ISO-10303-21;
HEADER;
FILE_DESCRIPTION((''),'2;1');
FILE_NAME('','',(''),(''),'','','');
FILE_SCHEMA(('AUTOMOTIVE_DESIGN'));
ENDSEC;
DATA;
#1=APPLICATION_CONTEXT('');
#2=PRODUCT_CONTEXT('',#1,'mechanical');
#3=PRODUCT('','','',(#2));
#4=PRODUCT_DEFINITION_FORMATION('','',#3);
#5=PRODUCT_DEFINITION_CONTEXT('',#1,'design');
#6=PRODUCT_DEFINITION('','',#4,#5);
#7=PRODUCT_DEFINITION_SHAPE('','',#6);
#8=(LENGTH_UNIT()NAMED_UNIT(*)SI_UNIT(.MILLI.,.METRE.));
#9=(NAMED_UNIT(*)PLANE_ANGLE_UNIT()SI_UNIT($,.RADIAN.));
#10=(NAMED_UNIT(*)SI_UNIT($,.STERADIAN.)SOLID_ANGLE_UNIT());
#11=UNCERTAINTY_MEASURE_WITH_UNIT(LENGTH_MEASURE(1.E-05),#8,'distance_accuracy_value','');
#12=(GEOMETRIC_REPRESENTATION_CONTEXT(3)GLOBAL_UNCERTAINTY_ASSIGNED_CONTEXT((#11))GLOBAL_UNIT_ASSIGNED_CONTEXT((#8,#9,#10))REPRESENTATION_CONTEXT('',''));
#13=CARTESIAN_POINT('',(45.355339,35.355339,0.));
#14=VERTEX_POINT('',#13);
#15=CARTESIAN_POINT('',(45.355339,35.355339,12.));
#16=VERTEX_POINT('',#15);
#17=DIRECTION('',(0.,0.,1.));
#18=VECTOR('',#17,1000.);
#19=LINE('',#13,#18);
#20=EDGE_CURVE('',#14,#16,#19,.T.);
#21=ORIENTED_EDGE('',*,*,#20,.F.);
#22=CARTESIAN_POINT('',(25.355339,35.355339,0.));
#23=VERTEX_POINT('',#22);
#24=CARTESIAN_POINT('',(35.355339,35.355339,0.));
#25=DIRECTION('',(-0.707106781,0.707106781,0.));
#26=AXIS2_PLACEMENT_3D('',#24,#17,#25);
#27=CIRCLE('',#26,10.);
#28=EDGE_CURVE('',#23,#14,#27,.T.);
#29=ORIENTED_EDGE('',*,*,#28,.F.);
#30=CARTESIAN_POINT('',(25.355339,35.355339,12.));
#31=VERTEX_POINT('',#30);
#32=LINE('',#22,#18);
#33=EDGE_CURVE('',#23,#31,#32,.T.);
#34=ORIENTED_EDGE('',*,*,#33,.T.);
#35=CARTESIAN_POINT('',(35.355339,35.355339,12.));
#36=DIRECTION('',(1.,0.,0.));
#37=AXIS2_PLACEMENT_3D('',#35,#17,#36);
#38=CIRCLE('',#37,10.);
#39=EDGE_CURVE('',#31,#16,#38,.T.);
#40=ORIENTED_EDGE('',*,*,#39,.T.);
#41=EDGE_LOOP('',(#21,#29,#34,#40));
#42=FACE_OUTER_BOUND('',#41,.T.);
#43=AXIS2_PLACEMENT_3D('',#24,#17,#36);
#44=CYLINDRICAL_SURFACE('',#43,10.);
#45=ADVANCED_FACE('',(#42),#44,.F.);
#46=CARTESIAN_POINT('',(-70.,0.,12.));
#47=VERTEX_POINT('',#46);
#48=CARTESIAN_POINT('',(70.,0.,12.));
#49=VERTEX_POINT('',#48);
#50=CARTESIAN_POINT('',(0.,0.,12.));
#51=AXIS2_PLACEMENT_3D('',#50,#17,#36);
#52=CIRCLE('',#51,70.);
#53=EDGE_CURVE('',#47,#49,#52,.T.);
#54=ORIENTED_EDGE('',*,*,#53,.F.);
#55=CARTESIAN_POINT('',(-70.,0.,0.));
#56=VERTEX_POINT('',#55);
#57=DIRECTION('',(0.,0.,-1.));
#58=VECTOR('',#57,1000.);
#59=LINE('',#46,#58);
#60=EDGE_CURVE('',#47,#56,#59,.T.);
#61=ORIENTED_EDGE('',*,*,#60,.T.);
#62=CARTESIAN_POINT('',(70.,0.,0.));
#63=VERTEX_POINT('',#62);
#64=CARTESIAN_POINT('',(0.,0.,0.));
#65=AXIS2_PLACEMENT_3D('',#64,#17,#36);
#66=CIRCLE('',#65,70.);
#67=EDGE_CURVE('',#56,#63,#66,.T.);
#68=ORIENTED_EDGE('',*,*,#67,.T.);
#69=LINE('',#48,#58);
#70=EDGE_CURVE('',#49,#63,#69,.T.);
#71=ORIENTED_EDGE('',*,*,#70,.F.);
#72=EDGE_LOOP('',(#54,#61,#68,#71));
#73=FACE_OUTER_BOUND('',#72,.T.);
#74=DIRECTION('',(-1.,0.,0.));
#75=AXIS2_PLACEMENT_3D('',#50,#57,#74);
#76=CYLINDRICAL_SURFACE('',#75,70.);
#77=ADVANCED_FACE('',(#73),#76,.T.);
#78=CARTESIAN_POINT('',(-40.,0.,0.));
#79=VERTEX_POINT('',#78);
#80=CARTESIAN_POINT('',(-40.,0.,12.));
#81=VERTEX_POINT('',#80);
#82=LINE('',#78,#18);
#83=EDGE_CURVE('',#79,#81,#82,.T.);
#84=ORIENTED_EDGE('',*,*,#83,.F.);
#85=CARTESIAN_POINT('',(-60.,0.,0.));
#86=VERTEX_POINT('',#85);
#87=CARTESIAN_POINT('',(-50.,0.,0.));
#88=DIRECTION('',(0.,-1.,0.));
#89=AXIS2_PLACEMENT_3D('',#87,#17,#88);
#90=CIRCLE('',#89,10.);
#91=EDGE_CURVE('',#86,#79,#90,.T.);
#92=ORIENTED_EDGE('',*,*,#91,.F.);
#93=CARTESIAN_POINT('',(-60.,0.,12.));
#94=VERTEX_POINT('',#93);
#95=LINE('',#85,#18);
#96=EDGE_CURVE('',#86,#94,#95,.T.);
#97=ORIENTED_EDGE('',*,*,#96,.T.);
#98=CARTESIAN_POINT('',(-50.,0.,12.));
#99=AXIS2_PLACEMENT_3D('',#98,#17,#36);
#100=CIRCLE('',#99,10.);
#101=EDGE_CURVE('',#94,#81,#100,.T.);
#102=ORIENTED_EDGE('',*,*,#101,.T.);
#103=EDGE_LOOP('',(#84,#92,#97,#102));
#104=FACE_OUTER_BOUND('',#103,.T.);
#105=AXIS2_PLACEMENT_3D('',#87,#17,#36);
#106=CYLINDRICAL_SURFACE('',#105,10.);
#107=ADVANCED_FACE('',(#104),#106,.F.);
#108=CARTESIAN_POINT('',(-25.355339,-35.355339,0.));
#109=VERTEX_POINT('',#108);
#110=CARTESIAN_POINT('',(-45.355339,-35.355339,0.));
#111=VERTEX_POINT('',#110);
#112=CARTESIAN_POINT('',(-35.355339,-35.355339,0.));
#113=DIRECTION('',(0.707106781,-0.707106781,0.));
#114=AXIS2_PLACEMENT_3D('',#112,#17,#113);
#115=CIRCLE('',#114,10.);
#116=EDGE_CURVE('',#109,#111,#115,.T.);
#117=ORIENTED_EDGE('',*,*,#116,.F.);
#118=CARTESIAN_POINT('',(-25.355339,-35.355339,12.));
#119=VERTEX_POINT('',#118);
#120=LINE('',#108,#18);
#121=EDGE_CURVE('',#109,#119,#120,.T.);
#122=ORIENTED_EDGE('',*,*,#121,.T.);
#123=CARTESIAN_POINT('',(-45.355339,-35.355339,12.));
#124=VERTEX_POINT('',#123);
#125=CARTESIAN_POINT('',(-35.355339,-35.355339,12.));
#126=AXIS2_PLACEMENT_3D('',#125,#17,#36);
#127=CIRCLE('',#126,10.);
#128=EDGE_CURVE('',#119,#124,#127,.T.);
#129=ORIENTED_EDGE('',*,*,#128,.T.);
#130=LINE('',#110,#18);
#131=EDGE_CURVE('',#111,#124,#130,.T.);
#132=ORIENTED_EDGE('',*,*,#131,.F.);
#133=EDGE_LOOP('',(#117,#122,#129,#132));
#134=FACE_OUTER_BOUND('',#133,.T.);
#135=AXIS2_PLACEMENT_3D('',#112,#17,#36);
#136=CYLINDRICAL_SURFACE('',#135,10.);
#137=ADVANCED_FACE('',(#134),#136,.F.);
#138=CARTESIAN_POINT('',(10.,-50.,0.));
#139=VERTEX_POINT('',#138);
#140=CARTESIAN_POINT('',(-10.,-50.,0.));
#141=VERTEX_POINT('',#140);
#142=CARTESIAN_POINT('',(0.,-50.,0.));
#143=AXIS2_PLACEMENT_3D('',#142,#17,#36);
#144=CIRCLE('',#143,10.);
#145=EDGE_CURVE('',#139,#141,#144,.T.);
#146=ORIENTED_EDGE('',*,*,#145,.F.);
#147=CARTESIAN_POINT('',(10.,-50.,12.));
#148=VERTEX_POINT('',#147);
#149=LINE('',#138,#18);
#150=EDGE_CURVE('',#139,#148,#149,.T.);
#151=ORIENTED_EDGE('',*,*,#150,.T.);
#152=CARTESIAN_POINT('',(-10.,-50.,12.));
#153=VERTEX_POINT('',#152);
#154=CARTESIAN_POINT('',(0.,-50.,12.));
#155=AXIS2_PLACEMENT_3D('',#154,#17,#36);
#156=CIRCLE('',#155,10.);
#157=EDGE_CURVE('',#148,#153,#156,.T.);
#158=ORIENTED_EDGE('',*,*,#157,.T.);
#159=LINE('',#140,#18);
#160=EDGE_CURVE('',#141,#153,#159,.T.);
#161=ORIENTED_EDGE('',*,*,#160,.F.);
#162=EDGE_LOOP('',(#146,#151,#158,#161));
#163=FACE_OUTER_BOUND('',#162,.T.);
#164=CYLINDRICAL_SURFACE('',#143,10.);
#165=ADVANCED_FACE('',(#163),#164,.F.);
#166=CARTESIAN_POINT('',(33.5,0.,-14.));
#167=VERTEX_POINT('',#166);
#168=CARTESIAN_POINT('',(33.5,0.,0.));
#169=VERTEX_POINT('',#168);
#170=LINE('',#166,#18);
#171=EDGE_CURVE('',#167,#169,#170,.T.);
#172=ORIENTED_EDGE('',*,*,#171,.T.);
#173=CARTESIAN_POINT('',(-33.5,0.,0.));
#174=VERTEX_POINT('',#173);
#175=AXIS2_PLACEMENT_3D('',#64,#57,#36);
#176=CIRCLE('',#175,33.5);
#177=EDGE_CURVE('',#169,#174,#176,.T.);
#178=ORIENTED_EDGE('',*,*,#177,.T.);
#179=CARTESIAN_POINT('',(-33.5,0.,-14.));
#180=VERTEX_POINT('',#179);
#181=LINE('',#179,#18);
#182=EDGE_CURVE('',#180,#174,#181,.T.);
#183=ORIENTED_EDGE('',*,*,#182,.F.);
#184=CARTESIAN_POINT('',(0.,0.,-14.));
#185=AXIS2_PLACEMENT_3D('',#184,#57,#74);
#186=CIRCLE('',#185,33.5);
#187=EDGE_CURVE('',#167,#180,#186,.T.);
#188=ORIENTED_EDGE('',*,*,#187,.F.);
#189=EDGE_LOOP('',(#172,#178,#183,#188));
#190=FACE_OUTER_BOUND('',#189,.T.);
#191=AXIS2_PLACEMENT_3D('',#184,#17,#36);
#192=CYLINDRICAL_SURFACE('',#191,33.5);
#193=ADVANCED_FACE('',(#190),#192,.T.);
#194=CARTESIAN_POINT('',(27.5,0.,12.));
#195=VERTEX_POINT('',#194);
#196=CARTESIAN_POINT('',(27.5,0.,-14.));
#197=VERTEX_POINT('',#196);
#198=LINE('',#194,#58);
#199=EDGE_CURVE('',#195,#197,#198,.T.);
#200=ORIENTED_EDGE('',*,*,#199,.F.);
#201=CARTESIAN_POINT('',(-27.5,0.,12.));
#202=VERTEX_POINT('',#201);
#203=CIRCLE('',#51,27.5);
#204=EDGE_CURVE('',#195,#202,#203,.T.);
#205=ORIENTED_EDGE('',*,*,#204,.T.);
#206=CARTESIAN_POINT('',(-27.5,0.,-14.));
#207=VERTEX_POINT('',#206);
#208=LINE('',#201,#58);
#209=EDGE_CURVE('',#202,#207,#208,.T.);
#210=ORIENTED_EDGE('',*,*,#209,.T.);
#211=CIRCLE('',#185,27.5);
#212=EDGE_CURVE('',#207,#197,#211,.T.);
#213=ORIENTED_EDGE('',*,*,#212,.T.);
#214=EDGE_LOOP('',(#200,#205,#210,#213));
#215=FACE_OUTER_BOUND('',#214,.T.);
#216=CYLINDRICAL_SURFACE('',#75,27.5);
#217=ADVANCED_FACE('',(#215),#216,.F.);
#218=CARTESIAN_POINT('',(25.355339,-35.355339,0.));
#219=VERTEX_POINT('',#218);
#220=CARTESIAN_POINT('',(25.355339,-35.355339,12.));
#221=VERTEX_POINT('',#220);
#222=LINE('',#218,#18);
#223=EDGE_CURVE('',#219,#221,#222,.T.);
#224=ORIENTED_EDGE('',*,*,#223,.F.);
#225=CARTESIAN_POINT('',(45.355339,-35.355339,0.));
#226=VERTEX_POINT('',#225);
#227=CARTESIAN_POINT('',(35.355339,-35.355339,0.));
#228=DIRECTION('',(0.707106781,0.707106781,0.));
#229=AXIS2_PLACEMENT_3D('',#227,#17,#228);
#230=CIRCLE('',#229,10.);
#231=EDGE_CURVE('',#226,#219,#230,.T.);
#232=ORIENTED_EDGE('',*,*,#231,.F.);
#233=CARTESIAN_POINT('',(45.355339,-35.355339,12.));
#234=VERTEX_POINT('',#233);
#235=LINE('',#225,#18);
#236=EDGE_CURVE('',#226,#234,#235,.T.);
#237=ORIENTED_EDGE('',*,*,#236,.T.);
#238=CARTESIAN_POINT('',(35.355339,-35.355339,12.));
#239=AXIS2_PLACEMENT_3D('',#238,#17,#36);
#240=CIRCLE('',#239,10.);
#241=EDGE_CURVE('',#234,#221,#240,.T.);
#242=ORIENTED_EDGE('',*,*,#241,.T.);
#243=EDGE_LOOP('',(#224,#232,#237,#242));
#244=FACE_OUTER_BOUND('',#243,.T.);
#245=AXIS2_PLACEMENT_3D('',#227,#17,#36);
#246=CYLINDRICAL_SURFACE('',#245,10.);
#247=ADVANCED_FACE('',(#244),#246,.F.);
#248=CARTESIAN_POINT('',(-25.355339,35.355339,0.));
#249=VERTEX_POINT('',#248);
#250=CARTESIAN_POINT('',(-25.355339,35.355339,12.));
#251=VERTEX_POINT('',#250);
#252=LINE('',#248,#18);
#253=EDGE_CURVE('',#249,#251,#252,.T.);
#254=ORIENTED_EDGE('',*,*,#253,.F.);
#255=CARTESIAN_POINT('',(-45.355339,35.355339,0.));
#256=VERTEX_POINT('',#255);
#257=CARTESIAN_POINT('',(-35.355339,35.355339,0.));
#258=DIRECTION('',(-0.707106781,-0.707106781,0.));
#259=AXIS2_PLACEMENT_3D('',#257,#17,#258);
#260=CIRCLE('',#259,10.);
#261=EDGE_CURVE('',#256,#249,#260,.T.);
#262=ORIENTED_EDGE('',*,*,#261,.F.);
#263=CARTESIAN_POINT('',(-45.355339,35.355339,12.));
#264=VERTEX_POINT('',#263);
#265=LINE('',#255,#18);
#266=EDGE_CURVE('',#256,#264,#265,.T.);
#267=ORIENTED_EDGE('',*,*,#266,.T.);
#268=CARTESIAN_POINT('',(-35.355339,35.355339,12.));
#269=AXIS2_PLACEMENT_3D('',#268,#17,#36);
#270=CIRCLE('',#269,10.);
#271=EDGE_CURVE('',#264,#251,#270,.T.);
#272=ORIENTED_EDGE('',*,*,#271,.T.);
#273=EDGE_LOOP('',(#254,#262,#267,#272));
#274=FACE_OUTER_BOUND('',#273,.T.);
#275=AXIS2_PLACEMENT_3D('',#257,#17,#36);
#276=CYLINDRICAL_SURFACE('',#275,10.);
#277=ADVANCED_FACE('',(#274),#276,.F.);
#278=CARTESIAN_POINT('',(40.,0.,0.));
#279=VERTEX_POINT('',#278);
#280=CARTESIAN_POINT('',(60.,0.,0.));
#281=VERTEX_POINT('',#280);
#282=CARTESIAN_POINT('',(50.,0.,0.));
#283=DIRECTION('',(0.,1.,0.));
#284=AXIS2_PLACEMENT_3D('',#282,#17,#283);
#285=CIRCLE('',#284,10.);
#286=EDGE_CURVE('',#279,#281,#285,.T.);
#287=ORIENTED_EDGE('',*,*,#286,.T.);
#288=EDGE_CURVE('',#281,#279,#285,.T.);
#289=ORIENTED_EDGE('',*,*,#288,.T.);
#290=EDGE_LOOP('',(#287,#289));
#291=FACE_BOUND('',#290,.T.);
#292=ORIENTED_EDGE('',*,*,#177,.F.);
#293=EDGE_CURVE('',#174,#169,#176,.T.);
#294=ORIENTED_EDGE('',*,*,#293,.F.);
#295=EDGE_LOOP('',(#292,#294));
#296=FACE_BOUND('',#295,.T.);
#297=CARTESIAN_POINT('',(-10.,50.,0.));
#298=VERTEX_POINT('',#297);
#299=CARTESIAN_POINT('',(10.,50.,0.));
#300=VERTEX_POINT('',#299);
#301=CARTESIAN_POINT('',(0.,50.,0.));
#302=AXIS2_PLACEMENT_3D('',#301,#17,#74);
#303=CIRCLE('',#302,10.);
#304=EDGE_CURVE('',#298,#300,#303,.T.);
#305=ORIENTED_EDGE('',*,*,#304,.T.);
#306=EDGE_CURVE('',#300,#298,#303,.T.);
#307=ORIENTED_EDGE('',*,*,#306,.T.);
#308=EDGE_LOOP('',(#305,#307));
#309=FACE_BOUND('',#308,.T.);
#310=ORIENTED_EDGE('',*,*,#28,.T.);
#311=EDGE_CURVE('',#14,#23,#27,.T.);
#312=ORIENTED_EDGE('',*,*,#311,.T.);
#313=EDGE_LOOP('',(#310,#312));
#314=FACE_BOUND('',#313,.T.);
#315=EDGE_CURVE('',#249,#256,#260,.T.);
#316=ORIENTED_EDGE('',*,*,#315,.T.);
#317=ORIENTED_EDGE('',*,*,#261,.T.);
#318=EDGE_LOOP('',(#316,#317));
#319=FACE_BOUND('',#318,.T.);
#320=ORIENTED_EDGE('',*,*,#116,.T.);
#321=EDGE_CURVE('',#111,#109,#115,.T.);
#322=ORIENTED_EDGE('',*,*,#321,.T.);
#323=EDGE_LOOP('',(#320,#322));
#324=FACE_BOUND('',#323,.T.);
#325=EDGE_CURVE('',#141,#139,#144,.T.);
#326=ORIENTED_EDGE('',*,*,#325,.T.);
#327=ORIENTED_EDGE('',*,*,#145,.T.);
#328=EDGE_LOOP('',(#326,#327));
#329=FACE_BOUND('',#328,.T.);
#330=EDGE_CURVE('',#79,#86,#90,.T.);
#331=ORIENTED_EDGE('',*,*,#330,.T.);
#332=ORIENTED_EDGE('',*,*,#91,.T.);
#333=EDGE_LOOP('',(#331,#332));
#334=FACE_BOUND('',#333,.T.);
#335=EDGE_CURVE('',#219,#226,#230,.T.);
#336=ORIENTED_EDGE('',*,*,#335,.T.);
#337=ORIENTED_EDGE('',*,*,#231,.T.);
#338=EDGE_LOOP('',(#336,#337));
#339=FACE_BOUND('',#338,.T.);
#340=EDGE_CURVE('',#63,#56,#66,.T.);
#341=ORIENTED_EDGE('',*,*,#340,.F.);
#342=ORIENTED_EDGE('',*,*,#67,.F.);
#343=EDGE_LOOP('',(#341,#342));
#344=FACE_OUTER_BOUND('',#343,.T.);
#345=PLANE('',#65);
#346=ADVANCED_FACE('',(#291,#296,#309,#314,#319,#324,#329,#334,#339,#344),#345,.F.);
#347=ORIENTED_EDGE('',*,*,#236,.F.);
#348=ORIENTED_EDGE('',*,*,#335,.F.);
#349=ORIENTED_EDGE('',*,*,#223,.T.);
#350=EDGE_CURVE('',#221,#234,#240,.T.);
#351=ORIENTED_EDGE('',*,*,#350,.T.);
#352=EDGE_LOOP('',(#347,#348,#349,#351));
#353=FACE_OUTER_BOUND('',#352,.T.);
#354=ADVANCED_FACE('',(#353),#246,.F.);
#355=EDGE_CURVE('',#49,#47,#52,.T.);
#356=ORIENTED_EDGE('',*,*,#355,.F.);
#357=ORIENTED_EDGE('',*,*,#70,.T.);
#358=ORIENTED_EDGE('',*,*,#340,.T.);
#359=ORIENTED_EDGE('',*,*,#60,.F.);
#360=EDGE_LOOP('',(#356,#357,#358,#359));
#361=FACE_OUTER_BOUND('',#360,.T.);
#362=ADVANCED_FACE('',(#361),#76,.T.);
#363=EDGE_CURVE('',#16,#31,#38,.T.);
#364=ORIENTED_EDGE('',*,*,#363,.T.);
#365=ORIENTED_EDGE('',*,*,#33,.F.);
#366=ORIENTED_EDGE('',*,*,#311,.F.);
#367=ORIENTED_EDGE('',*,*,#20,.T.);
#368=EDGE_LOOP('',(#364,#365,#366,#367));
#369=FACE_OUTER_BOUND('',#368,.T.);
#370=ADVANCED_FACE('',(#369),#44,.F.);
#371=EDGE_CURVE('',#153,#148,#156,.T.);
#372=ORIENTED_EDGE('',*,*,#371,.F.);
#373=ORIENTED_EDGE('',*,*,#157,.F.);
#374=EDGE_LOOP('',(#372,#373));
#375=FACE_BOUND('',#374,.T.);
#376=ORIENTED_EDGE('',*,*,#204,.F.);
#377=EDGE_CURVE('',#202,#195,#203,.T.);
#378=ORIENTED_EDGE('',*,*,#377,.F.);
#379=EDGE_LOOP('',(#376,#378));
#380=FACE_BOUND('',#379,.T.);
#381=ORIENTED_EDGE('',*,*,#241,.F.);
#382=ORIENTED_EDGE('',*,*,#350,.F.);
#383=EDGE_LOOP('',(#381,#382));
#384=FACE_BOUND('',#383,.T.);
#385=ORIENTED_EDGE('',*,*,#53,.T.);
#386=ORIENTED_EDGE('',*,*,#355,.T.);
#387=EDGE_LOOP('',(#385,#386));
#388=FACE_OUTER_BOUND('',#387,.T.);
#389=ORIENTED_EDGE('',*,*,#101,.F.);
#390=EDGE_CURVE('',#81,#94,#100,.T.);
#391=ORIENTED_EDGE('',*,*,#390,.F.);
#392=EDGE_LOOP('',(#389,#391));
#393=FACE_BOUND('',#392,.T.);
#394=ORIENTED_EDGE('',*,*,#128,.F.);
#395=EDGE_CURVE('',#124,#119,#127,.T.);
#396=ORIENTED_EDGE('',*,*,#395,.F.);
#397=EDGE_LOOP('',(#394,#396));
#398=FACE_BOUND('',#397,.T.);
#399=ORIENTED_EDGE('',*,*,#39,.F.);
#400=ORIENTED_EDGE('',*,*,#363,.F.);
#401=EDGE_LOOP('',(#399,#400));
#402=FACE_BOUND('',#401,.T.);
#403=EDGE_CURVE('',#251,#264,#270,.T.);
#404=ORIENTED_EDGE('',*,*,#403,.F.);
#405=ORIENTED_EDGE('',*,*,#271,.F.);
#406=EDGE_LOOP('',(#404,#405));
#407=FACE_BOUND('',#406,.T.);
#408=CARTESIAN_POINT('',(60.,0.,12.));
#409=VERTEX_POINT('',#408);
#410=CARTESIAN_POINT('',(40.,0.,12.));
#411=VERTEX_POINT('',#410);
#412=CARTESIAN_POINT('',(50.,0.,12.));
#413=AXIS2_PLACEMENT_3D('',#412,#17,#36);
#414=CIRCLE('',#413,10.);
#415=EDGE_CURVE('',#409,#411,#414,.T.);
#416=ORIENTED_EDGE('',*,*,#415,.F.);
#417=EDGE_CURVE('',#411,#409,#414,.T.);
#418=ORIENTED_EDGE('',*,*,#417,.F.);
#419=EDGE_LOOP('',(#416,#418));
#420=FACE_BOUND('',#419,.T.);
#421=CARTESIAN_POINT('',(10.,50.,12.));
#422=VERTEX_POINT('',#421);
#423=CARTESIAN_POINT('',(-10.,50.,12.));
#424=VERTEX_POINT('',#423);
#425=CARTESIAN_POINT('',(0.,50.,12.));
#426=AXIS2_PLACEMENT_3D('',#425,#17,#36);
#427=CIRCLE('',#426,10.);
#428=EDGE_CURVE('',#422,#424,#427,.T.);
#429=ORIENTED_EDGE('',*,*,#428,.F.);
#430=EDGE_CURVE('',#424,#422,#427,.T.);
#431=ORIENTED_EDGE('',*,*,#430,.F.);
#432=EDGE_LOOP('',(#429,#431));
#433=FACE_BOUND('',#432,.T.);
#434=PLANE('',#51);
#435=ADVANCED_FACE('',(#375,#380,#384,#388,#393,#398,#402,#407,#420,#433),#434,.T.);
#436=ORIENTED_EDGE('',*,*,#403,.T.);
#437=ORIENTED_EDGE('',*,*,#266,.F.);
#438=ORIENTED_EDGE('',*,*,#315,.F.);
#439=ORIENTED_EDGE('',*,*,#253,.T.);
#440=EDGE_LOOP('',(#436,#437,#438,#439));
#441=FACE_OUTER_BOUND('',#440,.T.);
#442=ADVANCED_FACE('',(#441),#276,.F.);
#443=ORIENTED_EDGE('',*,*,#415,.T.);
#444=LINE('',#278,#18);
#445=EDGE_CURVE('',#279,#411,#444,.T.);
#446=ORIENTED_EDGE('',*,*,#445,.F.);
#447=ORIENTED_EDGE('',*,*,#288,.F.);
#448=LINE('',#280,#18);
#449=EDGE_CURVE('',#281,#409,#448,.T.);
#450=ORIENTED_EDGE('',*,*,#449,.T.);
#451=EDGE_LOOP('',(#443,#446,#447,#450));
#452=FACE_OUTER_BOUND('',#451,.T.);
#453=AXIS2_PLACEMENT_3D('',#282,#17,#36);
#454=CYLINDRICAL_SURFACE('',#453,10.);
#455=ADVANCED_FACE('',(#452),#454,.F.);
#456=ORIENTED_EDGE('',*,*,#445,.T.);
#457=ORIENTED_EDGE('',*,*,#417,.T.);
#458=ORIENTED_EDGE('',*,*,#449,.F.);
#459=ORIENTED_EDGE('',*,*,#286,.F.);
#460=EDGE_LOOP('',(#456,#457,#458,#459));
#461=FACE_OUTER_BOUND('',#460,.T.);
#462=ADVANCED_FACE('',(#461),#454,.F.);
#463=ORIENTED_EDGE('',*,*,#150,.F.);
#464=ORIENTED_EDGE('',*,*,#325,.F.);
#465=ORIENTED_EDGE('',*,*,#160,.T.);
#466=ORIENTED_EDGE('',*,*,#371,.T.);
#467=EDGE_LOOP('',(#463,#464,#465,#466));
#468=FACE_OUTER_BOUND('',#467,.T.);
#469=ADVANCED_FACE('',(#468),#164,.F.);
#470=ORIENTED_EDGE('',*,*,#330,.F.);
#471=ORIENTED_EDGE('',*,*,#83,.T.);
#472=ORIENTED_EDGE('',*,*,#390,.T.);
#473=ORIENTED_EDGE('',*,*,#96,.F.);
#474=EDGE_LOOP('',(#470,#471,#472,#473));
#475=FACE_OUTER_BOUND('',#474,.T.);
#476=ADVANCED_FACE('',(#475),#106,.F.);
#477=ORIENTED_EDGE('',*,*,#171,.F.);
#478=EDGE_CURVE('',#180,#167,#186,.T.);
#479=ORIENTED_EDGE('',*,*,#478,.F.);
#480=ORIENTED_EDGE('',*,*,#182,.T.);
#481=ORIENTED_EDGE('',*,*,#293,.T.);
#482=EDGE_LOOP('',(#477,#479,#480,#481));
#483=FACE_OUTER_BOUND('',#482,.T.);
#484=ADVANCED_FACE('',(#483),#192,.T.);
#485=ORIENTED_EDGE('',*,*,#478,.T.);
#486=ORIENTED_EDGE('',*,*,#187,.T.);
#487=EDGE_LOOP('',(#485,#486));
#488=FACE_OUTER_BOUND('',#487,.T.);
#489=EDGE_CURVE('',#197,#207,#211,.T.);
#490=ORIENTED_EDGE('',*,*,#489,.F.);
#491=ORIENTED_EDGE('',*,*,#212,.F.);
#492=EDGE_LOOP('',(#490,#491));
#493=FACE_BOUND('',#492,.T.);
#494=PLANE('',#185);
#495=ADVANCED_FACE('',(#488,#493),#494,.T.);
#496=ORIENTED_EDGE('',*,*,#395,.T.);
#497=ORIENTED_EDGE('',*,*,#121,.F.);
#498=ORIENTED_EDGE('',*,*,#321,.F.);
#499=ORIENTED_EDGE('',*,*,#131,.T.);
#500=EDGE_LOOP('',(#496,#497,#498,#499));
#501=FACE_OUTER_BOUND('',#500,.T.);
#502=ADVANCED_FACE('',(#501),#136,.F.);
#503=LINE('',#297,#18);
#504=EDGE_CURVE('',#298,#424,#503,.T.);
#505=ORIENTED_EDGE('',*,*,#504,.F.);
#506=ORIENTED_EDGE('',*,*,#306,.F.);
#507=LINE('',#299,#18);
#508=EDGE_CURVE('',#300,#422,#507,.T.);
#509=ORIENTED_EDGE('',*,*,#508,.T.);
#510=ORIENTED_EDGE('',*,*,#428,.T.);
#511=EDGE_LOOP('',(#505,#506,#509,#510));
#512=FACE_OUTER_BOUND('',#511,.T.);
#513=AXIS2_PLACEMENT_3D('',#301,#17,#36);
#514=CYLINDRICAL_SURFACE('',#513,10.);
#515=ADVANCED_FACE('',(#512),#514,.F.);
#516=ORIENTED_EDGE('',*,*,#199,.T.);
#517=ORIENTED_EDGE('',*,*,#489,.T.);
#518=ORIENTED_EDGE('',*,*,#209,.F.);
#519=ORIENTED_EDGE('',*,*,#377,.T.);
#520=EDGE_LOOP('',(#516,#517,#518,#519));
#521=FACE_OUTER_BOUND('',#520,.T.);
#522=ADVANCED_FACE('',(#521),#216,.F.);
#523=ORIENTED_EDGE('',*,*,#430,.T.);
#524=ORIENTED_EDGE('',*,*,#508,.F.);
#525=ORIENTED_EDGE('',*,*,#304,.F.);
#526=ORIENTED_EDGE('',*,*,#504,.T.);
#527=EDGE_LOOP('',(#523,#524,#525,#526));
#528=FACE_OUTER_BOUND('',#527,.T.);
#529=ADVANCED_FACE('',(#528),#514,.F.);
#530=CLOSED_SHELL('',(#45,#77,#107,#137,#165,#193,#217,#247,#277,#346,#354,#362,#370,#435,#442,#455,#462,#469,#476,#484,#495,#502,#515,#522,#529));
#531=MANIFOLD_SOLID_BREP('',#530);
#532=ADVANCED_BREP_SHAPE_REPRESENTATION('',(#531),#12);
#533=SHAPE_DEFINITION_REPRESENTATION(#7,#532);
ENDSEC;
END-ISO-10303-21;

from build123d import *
from build123d.topology import SkipClean

# Parameters (mm, degrees)
SKETCH2_R           = 70
SKETCH2_R_2         = 27.5
BOSS_EXTRUDE1_DEPTH = 12
SKETCH3_R           = 10
CUT_EXTRUDE1_DEPTH  = 100.719606899
CIRPATTERN1_COUNT   = 8
BOSS_EXTRUDE2_START = 14
SKETCH4_R           = 33.5
SKETCH4_R_2         = 27.5
BOSS_EXTRUDE2_DEPTH = 14


with BuildPart() as part:
    # Sketch2 → Boss-Extrude1 (new body)
    with BuildSketch(Plane.XY):
        Circle(SKETCH2_R)
        Circle(SKETCH2_R_2, mode=Mode.SUBTRACT)
    extrude(amount=BOSS_EXTRUDE1_DEPTH)

    # Sketch3 → Cut-Extrude1 (cut, symmetric)
    with BuildSketch(Plane.XY.offset(12)):
        with Locations((0, -50)):
            Circle(SKETCH3_R)
    cut_extrude1 = extrude(amount=CUT_EXTRUDE1_DEPTH, both=True, mode=Mode.SUBTRACT)

    # CirPattern1: Cut-Extrude1 ×8 about axis
    cirpattern1_axis = Axis((0, 0, 0), (0, 0, 1))
    for i in range(1, CIRPATTERN1_COUNT):
        add(cut_extrude1.rotate(cirpattern1_axis, i * 360 / CIRPATTERN1_COUNT), mode=Mode.SUBTRACT)

    # Sketch4 → Boss-Extrude2 (add)
    with SkipClean():  # the faces are left unmerged after this step: merging them gives an invalid solid
        with BuildSketch(Plane(origin=(0, 0, 0), x_dir=(-1, 0, 0), z_dir=(0, 0, -1)).offset(BOSS_EXTRUDE2_START)):
            with Locations(Location((0, 0, 0), (0, 0, 180))):
                Circle(SKETCH4_R)
            Circle(SKETCH4_R_2, mode=Mode.SUBTRACT)
        extrude(amount=-BOSS_EXTRUDE2_DEPTH)


solid = part.part
